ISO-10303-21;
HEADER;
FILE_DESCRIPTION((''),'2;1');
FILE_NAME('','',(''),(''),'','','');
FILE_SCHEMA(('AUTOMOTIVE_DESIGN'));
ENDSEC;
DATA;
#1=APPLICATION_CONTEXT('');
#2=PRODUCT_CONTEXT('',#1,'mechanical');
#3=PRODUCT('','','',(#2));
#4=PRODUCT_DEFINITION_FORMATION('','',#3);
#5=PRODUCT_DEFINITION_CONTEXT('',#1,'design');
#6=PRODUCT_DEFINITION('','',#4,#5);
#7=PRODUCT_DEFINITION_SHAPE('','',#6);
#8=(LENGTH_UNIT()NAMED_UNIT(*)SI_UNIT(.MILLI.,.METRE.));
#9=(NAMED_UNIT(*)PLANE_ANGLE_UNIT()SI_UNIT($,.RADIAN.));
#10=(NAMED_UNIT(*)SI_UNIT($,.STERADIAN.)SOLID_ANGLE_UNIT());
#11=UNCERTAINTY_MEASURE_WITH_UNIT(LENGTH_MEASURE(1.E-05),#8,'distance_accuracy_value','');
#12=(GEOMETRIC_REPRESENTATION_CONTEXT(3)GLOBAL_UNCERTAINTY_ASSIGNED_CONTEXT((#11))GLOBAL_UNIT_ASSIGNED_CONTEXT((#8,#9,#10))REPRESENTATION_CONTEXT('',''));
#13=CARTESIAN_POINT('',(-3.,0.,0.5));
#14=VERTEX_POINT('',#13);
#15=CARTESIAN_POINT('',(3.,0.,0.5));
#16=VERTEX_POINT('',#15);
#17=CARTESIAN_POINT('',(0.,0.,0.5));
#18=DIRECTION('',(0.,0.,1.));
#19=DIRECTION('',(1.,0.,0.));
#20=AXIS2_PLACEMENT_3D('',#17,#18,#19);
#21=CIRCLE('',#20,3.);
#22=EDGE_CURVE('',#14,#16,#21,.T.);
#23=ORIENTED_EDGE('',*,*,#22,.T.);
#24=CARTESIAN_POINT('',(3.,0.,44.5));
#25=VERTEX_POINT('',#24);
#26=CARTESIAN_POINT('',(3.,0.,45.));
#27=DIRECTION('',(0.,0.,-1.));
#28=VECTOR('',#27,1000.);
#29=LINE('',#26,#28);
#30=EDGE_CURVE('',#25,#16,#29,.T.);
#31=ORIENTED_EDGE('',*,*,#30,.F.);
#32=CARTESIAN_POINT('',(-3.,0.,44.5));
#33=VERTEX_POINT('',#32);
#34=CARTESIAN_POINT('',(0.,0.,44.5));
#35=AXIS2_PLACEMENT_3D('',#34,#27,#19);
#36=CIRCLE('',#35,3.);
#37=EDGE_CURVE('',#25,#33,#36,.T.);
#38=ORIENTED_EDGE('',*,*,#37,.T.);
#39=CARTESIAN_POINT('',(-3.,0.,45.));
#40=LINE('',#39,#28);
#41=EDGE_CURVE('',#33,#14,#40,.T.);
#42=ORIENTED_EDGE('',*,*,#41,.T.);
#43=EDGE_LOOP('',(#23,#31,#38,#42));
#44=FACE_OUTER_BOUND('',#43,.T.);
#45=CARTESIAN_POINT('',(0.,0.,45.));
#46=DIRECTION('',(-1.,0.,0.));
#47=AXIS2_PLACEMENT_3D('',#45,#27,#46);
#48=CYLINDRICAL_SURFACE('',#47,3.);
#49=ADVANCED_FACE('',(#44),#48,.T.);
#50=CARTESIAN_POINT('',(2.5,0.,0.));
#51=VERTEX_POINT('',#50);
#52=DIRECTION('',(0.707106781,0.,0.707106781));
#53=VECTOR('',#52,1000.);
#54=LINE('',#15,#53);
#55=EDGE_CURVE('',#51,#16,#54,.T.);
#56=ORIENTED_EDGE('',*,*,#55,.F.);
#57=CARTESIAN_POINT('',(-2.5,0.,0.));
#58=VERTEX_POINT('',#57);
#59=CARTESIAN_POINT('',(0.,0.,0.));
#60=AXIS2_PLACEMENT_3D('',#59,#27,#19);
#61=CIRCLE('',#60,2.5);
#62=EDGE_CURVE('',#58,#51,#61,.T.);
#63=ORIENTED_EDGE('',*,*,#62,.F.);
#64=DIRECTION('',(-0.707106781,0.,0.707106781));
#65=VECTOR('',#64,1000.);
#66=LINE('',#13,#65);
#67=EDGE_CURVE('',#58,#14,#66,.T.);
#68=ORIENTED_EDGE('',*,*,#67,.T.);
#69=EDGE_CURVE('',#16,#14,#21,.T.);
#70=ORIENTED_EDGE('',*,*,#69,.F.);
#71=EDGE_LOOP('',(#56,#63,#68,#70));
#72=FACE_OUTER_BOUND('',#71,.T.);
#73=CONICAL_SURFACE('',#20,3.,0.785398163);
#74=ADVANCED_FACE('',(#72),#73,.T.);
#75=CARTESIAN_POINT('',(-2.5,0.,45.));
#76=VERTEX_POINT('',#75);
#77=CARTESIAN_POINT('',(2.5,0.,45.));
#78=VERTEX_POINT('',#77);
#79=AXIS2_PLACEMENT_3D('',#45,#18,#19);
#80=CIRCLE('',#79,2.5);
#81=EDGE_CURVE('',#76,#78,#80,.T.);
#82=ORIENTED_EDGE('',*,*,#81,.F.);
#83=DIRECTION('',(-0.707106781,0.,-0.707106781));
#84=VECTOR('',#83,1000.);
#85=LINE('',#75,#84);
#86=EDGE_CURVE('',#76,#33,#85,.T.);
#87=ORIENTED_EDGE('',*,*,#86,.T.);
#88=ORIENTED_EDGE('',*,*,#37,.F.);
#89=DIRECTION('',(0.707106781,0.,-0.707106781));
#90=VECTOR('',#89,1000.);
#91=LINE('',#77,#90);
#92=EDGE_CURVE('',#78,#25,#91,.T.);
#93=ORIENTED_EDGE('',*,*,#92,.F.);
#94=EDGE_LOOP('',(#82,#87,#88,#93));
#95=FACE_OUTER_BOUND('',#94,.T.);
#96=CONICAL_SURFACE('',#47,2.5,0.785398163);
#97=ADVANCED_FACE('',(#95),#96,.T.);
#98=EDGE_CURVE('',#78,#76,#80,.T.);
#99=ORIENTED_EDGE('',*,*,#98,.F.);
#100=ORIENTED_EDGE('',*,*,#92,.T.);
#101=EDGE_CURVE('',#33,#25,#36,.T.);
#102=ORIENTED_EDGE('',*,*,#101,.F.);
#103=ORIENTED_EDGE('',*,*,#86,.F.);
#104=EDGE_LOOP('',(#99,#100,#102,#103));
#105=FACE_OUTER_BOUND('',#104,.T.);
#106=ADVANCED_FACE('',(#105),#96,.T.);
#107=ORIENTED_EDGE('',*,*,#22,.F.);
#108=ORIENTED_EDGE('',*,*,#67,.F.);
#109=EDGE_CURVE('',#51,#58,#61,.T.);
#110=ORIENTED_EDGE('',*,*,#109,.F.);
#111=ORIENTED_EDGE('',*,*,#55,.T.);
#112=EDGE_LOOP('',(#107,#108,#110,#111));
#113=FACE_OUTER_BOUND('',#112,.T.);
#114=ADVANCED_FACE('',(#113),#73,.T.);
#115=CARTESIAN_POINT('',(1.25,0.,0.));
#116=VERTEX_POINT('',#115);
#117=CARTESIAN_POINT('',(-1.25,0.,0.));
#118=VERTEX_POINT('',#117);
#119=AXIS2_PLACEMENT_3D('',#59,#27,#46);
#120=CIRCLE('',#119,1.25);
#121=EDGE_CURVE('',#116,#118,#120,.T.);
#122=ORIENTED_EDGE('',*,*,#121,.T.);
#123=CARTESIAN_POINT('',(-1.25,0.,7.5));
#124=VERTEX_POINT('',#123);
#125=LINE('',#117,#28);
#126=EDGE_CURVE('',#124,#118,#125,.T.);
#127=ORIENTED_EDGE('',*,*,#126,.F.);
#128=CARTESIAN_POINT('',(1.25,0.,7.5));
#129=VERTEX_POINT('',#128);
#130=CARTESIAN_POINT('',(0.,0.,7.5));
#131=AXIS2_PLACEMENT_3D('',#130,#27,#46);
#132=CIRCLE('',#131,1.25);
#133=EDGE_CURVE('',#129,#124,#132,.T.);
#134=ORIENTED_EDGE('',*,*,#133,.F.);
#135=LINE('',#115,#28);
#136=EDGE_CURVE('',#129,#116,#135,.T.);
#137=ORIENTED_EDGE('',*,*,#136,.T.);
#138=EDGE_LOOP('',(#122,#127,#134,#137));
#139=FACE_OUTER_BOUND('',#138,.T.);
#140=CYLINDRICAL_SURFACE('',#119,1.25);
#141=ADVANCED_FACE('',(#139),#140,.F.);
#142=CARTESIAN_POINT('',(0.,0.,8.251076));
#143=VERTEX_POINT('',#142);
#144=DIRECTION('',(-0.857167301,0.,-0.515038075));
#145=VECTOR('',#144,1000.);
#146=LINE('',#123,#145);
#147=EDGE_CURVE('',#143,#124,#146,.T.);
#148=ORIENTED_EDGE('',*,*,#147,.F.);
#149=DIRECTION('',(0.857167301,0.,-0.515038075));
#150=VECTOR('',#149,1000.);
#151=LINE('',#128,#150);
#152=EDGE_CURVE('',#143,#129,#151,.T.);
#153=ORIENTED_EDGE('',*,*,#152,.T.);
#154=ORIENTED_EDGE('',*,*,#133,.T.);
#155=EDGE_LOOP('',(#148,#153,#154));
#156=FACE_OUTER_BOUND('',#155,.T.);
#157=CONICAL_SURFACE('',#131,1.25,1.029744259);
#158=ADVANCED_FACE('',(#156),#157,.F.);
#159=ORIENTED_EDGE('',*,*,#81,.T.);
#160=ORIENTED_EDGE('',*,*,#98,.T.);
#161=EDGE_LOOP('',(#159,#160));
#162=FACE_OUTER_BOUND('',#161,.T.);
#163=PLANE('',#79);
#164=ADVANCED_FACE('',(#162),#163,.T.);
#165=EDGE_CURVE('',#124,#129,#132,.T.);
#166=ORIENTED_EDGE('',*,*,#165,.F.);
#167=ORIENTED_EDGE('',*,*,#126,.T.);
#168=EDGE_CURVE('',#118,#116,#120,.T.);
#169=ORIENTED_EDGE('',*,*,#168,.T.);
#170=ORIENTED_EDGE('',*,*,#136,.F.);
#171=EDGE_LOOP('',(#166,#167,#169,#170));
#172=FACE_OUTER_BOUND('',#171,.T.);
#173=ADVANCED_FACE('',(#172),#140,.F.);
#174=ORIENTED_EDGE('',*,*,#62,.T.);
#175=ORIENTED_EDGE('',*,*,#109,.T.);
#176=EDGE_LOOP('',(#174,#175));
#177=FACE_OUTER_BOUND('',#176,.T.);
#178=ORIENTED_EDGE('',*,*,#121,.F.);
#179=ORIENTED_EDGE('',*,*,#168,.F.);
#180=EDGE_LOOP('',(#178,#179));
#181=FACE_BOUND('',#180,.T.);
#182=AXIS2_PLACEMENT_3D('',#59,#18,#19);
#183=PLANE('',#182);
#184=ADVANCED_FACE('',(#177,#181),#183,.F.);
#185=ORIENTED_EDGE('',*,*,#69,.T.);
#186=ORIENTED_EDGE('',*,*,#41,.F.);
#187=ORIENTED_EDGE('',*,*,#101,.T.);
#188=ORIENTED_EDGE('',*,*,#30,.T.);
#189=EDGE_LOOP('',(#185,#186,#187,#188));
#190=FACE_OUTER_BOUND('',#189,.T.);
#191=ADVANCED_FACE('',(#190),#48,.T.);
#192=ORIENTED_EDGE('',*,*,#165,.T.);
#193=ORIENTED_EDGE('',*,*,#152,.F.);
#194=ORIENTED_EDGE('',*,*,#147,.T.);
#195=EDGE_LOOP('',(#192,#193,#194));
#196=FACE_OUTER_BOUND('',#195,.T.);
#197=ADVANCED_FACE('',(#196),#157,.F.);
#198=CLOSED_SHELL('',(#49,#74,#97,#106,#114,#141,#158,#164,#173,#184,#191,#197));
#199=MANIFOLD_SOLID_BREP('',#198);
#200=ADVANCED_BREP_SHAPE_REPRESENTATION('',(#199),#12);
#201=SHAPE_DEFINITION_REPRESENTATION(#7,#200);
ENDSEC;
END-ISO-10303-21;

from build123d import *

# Parameters (mm, degrees)
SKETCH_1_R             = 3
EXTRUDE_1_DEPTH        = 45
HOLE_WIZARD_M3_1_D     = 2.5
HOLE_WIZARD_M3_1_DEPTH = 7.5
HOLE_WIZARD_M3_1_TIP   = 0.751075774
CHAMFER_1_SIZE         = 0.5


with BuildPart() as part:
    # 草图1 → 凸台-拉伸1 (new body)
    with BuildSketch(Plane.XY):
        with Locations(Location((0, 0, 0), (0, 0, 180))):
            Circle(SKETCH_1_R)
    extrude(amount=EXTRUDE_1_DEPTH)

    # M3 螺纹孔1
    with Locations(Plane(origin=(0, 0, 0), x_dir=(-1, 0, 0), z_dir=(0, 0, -1))):
        with Locations((0, 0)):
            Hole(HOLE_WIZARD_M3_1_D / 2, depth=HOLE_WIZARD_M3_1_DEPTH)
            with Locations((0, 0, -(HOLE_WIZARD_M3_1_DEPTH + HOLE_WIZARD_M3_1_TIP / 2))):  # 118° drill point
                Cone(0, HOLE_WIZARD_M3_1_D / 2, HOLE_WIZARD_M3_1_TIP, mode=Mode.SUBTRACT)

    # 倒角1
    chamfer_1_edges = [part.edges().sort_by_distance(p)[0] for p in [
        (3, 0, 0),
        (3, 0, 45),
    ]]
    chamfer(chamfer_1_edges, length=CHAMFER_1_SIZE)


solid = part.part
